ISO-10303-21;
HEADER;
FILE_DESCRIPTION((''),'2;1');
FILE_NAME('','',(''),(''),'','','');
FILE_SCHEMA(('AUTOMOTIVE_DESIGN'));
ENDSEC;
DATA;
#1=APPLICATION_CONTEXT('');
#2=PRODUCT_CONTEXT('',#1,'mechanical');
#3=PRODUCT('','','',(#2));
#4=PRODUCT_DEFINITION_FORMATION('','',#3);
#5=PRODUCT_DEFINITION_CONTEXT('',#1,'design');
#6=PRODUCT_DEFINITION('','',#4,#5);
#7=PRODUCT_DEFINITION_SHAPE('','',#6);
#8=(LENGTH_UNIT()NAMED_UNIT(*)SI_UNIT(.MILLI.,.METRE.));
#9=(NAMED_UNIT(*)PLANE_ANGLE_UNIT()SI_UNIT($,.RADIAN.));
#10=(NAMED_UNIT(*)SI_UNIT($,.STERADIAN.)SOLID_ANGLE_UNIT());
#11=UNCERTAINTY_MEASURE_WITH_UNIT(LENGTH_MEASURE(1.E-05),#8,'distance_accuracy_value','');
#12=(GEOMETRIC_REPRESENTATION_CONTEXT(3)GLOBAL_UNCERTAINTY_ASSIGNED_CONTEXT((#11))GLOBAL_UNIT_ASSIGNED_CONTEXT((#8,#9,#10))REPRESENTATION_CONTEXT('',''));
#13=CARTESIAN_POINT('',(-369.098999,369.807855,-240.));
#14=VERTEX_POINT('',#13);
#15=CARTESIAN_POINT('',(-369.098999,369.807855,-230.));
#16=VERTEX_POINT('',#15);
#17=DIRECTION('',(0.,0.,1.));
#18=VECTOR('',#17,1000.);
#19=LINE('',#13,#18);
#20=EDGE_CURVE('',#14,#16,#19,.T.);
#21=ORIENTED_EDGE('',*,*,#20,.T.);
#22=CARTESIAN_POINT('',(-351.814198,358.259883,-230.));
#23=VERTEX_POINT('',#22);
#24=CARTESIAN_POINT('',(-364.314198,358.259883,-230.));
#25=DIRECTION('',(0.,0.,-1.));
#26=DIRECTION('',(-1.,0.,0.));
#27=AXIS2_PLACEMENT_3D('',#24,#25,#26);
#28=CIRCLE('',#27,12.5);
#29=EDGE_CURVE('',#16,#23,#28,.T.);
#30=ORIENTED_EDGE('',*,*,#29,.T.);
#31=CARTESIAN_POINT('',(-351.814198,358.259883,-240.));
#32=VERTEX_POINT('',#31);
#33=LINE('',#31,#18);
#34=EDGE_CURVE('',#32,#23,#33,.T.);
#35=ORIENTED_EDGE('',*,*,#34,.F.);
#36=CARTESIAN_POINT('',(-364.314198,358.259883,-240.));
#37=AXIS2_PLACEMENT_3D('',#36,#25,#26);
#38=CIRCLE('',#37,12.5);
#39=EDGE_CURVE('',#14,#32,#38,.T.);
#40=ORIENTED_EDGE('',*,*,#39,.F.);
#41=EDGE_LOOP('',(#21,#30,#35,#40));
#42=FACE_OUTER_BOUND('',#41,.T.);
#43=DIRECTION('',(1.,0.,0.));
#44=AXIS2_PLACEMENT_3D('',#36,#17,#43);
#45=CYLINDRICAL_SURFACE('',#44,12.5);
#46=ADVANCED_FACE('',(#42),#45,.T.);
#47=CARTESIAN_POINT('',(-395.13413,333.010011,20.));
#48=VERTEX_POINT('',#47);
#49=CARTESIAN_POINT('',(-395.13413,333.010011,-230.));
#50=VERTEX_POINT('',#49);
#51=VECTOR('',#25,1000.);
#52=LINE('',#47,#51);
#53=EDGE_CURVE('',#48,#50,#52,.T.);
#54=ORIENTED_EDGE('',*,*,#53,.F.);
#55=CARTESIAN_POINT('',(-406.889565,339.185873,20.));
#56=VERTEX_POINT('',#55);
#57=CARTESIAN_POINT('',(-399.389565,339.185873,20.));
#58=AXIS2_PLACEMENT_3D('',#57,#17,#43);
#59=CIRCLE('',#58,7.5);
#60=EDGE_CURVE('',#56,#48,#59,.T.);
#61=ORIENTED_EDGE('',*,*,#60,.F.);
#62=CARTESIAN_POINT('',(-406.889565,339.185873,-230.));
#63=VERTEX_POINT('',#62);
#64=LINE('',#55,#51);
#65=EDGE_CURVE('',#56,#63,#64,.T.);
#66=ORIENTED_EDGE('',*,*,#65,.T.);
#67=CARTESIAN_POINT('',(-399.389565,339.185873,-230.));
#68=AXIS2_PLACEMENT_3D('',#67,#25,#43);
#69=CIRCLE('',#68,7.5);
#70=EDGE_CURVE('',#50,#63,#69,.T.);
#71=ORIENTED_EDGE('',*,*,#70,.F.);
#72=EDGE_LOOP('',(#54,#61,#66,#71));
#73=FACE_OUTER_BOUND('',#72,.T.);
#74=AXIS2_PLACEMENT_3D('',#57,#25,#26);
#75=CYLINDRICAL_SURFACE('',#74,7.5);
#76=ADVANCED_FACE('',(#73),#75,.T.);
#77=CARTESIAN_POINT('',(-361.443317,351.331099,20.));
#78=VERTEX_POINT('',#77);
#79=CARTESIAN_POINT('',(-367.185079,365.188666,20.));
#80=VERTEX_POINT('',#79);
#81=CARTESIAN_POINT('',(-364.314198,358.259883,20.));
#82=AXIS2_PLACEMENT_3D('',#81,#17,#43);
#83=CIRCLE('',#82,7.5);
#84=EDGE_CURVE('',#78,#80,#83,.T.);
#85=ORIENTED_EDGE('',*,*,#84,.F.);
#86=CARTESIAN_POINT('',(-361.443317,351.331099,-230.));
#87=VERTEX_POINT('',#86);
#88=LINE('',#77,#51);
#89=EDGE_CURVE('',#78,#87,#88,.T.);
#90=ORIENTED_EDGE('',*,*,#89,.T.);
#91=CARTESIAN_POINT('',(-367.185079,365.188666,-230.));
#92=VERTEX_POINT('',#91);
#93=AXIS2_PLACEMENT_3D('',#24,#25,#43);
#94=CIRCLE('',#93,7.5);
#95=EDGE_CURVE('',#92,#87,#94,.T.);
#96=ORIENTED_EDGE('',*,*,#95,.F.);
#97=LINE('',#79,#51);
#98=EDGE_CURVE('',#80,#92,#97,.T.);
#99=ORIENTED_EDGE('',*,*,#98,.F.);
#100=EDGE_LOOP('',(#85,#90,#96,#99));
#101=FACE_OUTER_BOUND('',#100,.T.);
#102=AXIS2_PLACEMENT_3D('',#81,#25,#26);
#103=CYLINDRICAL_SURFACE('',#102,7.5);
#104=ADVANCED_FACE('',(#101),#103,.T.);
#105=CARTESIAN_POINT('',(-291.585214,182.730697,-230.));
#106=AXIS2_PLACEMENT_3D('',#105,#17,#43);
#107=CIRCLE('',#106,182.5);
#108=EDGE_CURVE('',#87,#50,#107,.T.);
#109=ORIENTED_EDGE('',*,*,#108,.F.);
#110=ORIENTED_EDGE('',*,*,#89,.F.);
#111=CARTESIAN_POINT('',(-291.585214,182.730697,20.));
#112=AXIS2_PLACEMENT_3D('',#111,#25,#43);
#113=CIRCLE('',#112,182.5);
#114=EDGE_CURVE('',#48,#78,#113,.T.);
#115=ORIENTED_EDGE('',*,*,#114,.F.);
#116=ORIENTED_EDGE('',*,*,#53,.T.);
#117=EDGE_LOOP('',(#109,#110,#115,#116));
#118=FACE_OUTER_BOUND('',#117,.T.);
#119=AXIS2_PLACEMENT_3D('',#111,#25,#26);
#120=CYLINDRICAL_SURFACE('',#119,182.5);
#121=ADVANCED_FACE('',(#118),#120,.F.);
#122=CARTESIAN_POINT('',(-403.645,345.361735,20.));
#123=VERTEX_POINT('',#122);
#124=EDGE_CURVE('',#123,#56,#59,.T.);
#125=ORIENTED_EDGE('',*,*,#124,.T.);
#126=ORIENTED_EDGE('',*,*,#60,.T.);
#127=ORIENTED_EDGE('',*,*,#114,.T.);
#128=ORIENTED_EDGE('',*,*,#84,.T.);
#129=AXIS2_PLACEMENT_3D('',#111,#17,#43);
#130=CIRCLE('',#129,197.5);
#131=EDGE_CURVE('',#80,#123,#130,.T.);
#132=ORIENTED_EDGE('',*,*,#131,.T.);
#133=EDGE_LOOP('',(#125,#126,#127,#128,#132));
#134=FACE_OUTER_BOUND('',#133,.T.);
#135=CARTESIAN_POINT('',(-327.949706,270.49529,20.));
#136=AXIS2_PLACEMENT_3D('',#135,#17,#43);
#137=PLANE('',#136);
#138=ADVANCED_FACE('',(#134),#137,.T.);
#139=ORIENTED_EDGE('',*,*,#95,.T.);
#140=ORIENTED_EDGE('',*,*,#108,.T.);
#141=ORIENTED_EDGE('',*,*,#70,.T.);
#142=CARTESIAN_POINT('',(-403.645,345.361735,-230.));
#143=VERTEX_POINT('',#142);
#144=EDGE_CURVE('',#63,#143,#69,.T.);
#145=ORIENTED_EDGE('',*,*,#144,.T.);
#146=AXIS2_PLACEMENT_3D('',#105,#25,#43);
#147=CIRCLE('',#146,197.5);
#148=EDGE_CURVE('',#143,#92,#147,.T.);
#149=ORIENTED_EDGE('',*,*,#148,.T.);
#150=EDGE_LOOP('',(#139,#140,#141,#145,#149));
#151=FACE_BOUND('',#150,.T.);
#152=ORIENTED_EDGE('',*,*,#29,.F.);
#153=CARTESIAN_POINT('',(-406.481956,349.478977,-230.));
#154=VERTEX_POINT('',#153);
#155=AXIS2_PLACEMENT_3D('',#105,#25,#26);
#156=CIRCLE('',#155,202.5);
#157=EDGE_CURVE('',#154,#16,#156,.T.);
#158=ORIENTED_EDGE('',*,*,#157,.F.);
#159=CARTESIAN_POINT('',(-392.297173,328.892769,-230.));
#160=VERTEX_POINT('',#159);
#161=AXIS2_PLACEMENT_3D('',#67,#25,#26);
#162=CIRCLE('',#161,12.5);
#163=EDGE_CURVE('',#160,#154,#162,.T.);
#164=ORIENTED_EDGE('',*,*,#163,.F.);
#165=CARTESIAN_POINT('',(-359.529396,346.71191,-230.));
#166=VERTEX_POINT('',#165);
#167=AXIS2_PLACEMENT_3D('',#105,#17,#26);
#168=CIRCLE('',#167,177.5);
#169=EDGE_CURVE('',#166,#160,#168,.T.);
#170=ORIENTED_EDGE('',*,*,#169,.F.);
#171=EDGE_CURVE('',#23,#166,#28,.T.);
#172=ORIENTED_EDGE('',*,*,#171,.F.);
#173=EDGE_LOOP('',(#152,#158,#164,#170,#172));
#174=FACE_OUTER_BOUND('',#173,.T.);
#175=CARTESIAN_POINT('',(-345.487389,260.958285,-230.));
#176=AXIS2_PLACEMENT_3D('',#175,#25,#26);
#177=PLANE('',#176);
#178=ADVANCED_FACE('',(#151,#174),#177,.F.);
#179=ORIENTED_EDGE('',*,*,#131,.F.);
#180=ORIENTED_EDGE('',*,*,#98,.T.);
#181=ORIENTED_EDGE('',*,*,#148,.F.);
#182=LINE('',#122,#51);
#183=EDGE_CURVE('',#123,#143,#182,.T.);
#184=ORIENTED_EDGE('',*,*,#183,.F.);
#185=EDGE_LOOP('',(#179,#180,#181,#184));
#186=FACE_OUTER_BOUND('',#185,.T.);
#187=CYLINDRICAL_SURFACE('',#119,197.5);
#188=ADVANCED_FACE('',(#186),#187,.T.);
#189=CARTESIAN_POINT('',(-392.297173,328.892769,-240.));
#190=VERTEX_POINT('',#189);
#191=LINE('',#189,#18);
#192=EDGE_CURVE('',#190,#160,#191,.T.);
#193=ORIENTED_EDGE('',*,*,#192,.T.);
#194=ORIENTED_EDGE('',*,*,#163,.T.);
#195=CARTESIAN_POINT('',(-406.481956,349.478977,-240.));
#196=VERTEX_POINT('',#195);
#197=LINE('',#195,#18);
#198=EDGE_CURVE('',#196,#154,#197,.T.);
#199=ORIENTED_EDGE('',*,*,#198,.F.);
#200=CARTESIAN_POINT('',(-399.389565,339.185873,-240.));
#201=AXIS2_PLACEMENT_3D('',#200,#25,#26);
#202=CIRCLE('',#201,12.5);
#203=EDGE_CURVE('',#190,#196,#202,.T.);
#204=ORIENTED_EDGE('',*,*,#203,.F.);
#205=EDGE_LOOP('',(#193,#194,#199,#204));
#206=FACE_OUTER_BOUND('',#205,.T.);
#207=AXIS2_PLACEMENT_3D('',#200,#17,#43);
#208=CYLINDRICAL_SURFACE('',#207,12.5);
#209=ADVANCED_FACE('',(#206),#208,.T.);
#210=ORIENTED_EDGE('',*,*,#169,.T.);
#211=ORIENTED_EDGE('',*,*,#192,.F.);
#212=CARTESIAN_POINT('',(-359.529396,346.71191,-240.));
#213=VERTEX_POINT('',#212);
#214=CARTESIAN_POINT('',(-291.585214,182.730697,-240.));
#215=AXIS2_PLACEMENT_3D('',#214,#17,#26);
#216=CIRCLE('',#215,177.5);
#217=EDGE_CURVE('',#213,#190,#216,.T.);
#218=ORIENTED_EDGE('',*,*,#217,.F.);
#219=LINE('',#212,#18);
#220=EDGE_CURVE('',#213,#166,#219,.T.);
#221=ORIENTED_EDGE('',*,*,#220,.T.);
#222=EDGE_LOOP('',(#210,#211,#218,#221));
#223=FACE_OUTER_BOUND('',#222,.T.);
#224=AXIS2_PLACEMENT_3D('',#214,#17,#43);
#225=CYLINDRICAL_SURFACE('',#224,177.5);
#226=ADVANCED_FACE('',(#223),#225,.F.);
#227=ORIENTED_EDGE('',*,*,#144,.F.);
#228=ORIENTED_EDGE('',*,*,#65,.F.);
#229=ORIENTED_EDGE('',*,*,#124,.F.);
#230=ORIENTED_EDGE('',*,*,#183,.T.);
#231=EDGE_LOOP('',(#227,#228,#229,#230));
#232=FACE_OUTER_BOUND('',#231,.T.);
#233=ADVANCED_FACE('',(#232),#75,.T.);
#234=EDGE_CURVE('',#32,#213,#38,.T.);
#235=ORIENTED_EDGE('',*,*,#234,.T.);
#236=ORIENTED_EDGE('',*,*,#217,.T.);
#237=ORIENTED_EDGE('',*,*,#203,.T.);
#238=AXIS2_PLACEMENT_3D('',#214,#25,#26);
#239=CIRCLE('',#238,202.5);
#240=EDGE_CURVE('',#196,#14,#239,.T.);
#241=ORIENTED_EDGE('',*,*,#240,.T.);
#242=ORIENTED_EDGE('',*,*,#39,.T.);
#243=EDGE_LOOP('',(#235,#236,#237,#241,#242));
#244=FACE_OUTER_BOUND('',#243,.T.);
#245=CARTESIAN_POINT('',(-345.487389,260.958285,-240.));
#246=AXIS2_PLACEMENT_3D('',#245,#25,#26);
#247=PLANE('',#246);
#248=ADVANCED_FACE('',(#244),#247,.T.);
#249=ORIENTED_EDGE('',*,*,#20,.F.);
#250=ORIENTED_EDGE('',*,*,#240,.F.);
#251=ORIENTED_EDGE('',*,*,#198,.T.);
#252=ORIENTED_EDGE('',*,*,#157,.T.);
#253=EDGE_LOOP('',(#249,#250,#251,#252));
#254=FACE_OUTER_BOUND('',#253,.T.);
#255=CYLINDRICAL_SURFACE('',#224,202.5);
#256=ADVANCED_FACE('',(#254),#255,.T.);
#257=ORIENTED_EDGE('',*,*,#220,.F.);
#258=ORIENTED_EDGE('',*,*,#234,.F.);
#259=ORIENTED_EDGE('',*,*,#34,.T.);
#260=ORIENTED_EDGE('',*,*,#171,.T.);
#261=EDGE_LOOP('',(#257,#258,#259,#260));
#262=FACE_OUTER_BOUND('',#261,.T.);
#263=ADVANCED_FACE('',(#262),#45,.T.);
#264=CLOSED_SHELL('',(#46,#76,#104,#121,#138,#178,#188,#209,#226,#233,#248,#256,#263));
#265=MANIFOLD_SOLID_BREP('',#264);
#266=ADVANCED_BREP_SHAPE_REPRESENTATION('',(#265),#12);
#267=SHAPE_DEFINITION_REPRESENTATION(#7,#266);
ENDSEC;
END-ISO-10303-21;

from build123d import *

# Parameters (mm, degrees)
BOSS_EXTRUDE1_DEPTH      = 20
BOSS_EXTRUDE1_DEPTH_BACK = 230
BOSS_EXTRUDE2_DEPTH      = 10


with BuildPart() as part:
    # Sketch1 → Boss-Extrude1 (new, two sides: drawn at the far end of the back side and taken through both)
    with BuildSketch(Plane.XY.offset(-BOSS_EXTRUDE1_DEPTH_BACK)):
        with BuildLine():
            ThreePointArc((-367.185078684, 365.188666312), (-385.937282785, 356.235559249), (-403.644999576, 345.361735137))
            ThreePointArc((-403.644999576, 345.361735137), (-405.565426886, 334.930438049), (-395.134129798, 333.010010739))
            ThreePointArc((-395.134129798, 333.010010739), (-378.77130289, 343.057974791), (-361.443316822, 351.33109904))
            ThreePointArc((-361.443316822, 351.33109904), (-357.385414117, 361.130763607), (-367.185078684, 365.188666312))
        make_face()
    extrude(amount=BOSS_EXTRUDE1_DEPTH + BOSS_EXTRUDE1_DEPTH_BACK)

    # Sketch2 → Boss-Extrude2 (add)
    with BuildSketch(Plane(origin=(0, 0, -230), x_dir=(-1, 0, 0), z_dir=(0, 0, -1))):
        with BuildLine():
            ThreePointArc((406.481956169, 349.478976603), (388.32594275, 360.628087401), (369.098999305, 369.807855403))
            ThreePointArc((369.098999305, 369.807855403), (352.766225026, 363.044684228), (359.529396201, 346.711909949))
            ThreePointArc((359.529396201, 346.711909949), (376.382642925, 338.665446638), (392.297173205, 328.892769272))
            ThreePointArc((392.297173205, 328.892769272), (409.682668352, 332.093481456), (406.481956169, 349.478976603))
        make_face()
    extrude(amount=BOSS_EXTRUDE2_DEPTH)


solid = part.part
